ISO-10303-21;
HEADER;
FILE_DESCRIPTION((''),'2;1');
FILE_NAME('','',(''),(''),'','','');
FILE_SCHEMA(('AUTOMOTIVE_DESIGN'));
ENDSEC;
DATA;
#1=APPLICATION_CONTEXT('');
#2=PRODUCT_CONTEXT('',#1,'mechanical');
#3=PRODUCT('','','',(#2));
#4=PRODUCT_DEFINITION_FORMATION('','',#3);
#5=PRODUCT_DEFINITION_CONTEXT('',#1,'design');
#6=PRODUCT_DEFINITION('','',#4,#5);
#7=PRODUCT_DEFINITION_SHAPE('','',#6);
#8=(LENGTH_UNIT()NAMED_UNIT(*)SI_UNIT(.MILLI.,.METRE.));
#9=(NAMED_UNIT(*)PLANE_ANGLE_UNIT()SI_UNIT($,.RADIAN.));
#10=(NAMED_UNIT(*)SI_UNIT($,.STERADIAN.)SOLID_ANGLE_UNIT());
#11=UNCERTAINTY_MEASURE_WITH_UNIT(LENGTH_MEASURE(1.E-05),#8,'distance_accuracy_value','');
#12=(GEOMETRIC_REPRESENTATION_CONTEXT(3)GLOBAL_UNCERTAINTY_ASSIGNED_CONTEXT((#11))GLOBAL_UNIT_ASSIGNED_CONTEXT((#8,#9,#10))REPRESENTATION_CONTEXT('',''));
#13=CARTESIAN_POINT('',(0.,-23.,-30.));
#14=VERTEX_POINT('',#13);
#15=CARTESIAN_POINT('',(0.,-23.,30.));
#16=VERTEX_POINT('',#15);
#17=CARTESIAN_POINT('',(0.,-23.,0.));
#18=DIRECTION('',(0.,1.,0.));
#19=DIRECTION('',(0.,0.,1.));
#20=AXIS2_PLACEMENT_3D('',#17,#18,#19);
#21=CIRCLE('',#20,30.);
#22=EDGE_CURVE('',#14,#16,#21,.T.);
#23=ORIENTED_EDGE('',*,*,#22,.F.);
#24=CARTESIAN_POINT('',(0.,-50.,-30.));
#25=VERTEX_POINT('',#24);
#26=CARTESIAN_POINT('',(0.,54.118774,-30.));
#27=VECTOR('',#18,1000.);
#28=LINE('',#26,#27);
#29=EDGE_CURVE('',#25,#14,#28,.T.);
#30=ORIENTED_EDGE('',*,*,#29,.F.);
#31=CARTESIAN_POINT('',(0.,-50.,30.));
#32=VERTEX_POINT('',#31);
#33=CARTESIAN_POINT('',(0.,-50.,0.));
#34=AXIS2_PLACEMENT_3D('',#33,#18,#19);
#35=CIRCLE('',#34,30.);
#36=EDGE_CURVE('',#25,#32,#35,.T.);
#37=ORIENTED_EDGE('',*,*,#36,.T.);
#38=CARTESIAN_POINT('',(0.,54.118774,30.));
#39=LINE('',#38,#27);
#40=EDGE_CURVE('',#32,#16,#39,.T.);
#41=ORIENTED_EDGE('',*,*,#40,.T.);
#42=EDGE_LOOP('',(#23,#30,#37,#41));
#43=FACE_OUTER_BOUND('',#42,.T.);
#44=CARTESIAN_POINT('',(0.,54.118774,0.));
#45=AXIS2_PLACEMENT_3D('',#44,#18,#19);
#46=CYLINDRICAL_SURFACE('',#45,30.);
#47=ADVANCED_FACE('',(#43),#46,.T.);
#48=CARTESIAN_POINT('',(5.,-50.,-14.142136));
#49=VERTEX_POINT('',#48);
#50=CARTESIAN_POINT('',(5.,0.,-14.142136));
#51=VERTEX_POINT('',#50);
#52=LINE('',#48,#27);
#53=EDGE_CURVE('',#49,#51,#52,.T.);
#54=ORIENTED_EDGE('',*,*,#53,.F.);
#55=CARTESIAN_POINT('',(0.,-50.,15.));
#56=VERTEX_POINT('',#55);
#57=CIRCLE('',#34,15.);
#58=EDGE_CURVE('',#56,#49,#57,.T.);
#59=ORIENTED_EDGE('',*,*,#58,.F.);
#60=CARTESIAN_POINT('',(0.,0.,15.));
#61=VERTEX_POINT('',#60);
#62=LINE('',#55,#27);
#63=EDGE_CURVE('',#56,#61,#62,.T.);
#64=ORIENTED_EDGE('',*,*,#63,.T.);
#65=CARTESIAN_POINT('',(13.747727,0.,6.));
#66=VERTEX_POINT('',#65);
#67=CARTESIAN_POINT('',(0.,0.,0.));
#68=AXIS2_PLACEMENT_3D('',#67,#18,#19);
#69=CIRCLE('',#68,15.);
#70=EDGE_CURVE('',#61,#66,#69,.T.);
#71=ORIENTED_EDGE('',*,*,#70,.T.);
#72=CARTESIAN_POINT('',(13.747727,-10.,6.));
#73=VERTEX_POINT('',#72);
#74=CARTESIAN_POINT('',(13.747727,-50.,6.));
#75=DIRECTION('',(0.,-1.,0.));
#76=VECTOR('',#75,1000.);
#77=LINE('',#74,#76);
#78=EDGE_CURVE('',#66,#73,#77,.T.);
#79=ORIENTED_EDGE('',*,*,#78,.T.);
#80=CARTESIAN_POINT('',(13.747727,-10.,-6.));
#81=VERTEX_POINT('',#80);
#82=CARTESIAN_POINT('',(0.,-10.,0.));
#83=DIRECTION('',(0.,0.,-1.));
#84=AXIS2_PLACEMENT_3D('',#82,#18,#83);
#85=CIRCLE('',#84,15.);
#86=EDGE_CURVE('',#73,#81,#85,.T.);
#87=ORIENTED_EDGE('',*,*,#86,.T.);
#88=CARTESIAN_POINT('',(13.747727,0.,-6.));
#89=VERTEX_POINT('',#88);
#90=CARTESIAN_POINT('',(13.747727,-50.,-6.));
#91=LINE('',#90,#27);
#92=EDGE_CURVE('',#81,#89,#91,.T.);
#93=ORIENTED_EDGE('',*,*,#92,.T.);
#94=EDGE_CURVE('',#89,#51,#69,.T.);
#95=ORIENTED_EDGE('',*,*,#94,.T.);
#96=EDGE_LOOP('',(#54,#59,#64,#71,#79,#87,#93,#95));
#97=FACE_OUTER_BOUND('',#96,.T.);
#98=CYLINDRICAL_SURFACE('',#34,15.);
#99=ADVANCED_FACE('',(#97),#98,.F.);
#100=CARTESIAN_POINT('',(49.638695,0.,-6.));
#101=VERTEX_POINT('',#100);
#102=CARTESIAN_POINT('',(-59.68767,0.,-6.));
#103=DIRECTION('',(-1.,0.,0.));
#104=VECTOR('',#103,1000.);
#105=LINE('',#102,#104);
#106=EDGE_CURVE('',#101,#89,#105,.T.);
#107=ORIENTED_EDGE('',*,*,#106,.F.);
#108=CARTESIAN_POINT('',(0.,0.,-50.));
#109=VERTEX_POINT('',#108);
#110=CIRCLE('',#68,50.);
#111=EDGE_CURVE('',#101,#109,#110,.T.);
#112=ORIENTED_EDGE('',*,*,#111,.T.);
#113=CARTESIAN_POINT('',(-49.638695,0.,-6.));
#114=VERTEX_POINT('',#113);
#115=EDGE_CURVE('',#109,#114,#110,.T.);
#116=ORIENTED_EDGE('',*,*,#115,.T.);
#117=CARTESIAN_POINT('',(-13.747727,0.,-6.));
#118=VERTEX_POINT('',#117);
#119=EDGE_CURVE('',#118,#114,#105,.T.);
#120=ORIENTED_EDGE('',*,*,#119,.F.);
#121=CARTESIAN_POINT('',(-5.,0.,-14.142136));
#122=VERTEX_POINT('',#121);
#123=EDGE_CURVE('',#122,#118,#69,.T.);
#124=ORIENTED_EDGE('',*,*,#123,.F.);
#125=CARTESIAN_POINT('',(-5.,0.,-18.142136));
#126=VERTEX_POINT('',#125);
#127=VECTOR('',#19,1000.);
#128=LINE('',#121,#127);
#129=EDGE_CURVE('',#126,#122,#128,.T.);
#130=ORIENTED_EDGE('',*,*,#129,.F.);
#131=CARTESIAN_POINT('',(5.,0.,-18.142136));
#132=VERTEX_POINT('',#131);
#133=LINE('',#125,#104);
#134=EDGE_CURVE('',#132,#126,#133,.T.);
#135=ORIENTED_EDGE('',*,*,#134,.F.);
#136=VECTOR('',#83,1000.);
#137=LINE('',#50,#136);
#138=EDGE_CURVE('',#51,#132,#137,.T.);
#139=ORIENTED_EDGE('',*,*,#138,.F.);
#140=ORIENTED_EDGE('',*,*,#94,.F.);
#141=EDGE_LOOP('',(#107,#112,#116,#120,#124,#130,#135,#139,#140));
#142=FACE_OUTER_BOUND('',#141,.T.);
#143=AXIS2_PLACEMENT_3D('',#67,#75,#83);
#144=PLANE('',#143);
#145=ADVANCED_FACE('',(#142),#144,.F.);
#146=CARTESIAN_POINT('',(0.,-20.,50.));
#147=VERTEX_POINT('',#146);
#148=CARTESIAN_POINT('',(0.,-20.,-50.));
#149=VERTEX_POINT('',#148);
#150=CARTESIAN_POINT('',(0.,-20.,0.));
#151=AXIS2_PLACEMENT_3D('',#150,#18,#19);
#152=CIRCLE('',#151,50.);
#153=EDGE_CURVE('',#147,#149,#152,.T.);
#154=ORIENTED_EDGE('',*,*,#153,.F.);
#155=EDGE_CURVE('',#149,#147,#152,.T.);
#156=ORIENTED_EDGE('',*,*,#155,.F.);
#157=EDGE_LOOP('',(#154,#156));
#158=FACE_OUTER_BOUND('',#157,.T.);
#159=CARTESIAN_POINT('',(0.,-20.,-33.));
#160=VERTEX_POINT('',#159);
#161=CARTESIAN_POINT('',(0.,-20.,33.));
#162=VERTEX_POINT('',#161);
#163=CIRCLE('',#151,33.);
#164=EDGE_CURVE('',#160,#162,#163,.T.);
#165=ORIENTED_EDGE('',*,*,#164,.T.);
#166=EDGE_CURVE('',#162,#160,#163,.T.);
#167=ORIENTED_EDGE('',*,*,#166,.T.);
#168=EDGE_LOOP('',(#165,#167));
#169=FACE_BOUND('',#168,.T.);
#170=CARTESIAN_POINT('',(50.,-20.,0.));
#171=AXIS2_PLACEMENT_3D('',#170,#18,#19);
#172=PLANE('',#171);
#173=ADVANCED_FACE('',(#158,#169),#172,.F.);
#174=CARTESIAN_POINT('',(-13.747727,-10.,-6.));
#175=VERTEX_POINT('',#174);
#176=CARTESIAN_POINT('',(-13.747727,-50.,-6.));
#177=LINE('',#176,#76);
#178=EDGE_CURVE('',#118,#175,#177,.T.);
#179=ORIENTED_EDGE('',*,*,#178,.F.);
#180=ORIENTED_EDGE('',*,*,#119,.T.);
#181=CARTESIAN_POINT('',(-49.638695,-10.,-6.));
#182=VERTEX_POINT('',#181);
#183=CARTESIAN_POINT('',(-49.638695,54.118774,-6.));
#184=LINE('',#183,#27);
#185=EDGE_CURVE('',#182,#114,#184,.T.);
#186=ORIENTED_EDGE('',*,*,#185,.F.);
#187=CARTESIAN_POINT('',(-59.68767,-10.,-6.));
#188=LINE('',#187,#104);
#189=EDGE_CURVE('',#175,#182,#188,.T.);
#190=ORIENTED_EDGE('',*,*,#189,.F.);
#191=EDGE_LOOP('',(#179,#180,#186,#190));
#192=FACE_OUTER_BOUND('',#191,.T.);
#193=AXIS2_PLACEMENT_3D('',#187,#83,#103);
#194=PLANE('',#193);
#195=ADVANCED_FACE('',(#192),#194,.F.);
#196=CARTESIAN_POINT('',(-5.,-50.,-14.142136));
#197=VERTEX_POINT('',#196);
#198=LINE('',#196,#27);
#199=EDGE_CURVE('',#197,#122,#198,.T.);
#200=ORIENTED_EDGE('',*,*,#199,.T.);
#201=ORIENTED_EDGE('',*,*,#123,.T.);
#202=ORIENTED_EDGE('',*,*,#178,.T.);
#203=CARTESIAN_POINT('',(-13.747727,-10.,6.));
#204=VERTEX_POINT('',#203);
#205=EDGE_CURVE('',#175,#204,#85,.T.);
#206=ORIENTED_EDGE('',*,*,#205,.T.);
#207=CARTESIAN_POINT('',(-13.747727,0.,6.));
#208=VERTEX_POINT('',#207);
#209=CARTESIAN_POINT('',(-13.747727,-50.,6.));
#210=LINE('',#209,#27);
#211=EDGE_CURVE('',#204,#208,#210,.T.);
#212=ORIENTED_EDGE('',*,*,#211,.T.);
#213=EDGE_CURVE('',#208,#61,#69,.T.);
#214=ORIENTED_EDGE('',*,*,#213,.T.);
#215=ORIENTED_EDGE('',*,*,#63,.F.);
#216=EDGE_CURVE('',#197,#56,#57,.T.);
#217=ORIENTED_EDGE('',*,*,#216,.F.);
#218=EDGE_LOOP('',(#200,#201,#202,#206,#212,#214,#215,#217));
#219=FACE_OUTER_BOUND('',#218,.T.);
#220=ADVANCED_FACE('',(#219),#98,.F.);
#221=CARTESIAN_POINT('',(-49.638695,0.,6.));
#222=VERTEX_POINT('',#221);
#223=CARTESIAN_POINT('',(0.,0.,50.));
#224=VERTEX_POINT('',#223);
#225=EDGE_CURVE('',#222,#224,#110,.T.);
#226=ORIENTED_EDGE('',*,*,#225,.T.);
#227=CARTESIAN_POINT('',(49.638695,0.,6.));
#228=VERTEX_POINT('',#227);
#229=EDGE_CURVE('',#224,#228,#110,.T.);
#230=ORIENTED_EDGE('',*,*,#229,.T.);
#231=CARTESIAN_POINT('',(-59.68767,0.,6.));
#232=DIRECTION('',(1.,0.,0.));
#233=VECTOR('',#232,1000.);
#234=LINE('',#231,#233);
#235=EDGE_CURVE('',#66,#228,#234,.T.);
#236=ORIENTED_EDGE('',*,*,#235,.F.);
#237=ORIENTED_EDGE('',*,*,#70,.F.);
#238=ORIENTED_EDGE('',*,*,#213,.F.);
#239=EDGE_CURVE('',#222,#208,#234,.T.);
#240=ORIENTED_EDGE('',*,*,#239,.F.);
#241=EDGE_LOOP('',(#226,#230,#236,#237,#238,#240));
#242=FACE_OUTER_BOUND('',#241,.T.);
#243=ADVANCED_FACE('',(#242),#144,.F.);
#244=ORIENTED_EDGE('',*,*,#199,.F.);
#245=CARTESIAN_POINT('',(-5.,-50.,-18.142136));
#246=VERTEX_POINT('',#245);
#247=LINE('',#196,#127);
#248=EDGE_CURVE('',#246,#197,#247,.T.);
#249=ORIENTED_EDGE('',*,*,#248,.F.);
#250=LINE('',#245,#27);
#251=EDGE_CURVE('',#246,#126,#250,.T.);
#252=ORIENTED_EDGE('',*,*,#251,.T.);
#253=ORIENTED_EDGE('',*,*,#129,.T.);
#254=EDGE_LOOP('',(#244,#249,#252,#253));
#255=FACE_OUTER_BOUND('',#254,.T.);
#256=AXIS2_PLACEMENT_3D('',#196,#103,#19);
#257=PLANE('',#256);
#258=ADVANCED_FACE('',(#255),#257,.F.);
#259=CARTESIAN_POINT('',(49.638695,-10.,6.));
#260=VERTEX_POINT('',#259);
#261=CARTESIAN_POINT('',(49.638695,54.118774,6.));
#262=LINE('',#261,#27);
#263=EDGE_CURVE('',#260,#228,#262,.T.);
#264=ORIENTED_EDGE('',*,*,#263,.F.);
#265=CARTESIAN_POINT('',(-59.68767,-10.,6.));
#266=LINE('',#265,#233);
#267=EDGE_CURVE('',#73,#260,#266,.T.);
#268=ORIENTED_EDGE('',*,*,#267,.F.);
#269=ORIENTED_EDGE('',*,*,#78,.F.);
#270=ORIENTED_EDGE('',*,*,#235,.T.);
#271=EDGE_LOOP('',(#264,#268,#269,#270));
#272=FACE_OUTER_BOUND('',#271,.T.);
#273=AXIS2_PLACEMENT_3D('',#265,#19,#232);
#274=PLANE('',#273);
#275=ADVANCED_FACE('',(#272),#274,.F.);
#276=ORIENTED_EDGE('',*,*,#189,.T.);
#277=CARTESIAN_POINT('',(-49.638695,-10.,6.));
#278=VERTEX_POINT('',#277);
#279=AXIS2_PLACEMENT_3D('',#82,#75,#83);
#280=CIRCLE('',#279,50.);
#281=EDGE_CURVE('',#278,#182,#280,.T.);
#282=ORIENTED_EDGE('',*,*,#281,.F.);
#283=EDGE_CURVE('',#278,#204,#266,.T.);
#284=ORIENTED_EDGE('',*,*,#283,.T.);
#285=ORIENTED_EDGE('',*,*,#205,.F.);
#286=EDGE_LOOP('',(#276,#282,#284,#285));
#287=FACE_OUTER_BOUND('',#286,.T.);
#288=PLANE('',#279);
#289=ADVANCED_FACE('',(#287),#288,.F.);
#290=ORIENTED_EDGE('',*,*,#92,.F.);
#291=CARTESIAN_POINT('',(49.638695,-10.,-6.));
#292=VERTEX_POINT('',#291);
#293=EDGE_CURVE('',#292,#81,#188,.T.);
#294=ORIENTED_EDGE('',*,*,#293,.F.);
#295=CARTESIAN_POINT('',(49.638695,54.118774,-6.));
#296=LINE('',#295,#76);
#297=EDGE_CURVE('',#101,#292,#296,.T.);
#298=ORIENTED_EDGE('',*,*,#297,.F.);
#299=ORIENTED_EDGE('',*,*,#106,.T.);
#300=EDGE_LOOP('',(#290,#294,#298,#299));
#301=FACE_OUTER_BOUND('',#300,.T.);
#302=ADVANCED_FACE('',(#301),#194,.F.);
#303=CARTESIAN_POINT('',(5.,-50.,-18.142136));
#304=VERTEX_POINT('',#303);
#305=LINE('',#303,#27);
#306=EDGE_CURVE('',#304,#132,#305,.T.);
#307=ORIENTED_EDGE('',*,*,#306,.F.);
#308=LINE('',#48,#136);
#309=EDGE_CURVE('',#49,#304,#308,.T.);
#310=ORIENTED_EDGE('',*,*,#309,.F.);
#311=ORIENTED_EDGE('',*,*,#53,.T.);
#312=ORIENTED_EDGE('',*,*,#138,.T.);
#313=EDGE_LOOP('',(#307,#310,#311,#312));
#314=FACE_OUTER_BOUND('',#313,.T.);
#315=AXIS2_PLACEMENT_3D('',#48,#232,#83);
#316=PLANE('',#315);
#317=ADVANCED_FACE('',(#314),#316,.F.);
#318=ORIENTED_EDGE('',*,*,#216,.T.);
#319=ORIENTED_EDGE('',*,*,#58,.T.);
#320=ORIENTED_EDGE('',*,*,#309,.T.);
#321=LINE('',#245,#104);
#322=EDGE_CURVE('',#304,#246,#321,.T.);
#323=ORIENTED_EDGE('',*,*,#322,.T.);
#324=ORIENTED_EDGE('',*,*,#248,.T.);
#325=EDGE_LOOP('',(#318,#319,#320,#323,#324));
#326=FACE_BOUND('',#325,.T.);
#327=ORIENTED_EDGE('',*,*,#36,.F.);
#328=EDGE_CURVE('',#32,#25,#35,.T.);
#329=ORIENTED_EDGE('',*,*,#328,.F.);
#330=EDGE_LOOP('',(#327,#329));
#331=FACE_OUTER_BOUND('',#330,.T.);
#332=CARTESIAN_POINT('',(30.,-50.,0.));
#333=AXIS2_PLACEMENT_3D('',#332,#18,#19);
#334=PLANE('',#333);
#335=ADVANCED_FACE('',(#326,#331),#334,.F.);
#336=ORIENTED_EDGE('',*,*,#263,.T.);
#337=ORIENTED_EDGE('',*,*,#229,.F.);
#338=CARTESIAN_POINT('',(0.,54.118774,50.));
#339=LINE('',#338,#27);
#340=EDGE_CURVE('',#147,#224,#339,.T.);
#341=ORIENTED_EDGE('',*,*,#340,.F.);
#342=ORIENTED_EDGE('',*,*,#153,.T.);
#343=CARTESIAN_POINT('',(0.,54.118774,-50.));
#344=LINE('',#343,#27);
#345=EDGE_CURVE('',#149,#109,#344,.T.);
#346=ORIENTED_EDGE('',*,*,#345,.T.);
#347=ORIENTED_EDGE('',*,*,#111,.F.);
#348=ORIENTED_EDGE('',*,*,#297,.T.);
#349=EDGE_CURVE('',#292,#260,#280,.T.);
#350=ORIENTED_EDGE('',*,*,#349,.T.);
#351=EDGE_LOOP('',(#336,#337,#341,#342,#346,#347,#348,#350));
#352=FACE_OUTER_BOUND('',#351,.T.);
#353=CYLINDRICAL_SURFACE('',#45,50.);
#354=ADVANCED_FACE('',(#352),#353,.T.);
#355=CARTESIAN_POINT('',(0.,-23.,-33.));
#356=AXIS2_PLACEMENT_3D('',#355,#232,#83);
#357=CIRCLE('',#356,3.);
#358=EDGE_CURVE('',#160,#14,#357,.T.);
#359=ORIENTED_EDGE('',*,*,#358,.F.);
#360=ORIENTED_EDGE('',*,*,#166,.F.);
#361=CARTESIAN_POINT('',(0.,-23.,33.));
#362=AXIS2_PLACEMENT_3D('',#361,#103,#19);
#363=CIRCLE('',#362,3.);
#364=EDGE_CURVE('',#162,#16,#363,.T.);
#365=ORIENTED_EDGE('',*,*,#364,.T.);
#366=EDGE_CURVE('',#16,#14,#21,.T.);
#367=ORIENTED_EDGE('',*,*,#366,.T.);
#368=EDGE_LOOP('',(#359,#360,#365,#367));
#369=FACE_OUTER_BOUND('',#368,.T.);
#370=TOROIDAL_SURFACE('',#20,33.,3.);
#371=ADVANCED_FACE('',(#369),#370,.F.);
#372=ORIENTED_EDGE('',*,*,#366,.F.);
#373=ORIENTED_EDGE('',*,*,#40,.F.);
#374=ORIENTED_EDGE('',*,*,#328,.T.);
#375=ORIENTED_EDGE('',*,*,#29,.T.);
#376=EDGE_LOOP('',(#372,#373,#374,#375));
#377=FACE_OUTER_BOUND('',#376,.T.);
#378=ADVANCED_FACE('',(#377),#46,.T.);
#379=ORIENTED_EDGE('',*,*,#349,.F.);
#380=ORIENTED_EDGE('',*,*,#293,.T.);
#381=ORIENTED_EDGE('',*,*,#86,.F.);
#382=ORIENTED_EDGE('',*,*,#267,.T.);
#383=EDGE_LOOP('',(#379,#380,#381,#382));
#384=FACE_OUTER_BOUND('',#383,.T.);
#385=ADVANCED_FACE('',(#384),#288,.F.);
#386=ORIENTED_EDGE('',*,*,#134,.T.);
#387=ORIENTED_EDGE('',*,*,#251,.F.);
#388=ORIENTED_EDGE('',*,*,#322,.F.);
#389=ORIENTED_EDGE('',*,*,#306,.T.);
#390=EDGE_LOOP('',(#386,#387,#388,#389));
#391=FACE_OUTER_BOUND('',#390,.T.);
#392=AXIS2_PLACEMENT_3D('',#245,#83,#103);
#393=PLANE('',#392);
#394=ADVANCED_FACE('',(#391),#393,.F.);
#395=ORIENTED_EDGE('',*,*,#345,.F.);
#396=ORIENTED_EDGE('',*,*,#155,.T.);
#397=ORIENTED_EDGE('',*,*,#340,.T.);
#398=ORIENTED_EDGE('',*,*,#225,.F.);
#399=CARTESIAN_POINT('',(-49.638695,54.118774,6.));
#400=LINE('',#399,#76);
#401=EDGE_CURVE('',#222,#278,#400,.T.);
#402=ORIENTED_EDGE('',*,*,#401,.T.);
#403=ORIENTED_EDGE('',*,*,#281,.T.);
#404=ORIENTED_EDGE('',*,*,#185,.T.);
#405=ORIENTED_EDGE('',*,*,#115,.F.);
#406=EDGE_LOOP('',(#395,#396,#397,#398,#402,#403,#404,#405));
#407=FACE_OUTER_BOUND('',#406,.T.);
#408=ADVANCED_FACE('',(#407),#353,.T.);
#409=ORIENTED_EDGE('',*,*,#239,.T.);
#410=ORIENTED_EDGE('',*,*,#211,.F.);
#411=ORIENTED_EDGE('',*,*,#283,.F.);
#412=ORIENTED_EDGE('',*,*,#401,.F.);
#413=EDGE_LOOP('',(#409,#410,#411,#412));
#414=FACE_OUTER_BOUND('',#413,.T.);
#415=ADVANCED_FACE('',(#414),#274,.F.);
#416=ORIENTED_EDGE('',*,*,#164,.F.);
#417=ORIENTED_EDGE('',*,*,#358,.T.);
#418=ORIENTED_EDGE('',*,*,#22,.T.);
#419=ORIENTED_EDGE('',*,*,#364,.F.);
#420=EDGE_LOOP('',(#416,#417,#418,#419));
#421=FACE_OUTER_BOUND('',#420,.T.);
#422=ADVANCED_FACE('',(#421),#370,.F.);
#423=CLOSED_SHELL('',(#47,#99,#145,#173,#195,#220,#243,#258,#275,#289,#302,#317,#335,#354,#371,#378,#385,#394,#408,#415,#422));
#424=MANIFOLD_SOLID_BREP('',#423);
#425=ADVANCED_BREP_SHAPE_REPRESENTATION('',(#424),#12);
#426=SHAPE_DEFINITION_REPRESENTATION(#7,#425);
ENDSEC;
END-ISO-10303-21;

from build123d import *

# Parameters (mm, degrees)
BORE_KEYWAY_4MM_DEPTH  = 87.602540378
CROSS_SLOT_SKETCH_W    = 119.375340358
CROSS_SLOT_SKETCH_H    = 12
CROSS_SLOT_12X10_DEPTH = 10


with BuildPart() as part:
    # Flange Profile Sketch → Flange Body Revolve (revolve)
    with BuildSketch(Plane.XY, mode=Mode.PRIVATE) as flange_body_revolve_sk:
        with BuildLine():
            Line((0, 0), (50, 0))
            Line((50, 0), (50, -20))
            Line((50, -20), (33, -20))
            ThreePointArc((33, -20), (30.878679656, -20.878679656), (30, -23))
            Line((30, -23), (30, -50))
            Line((30, -50), (0, -50))
            Line((0, -50), (0, 0))
        make_face()
    revolve(flange_body_revolve_sk.sketch.rotate(Axis((0, 54.118773946, 0), (0, -1, 0)), 90), axis=Axis((0, 54.118773946, 0), (0, -1, 0)))

    # Bore Keyway Sketch → Bore Keyway 4mm (cut, through all)
    with BuildSketch(Plane(origin=(0, 0, 0), x_dir=(1, 0, 0), z_dir=(0, 1, 0))):
        with BuildLine():
            Line((-5, 14.142135624), (-5, 18.142135624))
            Line((-5, 18.142135624), (5, 18.142135624))
            Line((5, 18.142135624), (5, 14.142135624))
            ThreePointArc((5, 14.142135624), (0, -15), (-5, 14.142135624))
        make_face()
    extrude(amount=-BORE_KEYWAY_4MM_DEPTH, mode=Mode.SUBTRACT)

    # Cross Slot Sketch → Cross Slot 12x10 (cut)
    with BuildSketch(Plane(origin=(0, 0, 0), x_dir=(1, 0, 0), z_dir=(0, 1, 0))):
        Rectangle(CROSS_SLOT_SKETCH_W, CROSS_SLOT_SKETCH_H)
    extrude(amount=-CROSS_SLOT_12X10_DEPTH, mode=Mode.SUBTRACT)


solid = part.part
